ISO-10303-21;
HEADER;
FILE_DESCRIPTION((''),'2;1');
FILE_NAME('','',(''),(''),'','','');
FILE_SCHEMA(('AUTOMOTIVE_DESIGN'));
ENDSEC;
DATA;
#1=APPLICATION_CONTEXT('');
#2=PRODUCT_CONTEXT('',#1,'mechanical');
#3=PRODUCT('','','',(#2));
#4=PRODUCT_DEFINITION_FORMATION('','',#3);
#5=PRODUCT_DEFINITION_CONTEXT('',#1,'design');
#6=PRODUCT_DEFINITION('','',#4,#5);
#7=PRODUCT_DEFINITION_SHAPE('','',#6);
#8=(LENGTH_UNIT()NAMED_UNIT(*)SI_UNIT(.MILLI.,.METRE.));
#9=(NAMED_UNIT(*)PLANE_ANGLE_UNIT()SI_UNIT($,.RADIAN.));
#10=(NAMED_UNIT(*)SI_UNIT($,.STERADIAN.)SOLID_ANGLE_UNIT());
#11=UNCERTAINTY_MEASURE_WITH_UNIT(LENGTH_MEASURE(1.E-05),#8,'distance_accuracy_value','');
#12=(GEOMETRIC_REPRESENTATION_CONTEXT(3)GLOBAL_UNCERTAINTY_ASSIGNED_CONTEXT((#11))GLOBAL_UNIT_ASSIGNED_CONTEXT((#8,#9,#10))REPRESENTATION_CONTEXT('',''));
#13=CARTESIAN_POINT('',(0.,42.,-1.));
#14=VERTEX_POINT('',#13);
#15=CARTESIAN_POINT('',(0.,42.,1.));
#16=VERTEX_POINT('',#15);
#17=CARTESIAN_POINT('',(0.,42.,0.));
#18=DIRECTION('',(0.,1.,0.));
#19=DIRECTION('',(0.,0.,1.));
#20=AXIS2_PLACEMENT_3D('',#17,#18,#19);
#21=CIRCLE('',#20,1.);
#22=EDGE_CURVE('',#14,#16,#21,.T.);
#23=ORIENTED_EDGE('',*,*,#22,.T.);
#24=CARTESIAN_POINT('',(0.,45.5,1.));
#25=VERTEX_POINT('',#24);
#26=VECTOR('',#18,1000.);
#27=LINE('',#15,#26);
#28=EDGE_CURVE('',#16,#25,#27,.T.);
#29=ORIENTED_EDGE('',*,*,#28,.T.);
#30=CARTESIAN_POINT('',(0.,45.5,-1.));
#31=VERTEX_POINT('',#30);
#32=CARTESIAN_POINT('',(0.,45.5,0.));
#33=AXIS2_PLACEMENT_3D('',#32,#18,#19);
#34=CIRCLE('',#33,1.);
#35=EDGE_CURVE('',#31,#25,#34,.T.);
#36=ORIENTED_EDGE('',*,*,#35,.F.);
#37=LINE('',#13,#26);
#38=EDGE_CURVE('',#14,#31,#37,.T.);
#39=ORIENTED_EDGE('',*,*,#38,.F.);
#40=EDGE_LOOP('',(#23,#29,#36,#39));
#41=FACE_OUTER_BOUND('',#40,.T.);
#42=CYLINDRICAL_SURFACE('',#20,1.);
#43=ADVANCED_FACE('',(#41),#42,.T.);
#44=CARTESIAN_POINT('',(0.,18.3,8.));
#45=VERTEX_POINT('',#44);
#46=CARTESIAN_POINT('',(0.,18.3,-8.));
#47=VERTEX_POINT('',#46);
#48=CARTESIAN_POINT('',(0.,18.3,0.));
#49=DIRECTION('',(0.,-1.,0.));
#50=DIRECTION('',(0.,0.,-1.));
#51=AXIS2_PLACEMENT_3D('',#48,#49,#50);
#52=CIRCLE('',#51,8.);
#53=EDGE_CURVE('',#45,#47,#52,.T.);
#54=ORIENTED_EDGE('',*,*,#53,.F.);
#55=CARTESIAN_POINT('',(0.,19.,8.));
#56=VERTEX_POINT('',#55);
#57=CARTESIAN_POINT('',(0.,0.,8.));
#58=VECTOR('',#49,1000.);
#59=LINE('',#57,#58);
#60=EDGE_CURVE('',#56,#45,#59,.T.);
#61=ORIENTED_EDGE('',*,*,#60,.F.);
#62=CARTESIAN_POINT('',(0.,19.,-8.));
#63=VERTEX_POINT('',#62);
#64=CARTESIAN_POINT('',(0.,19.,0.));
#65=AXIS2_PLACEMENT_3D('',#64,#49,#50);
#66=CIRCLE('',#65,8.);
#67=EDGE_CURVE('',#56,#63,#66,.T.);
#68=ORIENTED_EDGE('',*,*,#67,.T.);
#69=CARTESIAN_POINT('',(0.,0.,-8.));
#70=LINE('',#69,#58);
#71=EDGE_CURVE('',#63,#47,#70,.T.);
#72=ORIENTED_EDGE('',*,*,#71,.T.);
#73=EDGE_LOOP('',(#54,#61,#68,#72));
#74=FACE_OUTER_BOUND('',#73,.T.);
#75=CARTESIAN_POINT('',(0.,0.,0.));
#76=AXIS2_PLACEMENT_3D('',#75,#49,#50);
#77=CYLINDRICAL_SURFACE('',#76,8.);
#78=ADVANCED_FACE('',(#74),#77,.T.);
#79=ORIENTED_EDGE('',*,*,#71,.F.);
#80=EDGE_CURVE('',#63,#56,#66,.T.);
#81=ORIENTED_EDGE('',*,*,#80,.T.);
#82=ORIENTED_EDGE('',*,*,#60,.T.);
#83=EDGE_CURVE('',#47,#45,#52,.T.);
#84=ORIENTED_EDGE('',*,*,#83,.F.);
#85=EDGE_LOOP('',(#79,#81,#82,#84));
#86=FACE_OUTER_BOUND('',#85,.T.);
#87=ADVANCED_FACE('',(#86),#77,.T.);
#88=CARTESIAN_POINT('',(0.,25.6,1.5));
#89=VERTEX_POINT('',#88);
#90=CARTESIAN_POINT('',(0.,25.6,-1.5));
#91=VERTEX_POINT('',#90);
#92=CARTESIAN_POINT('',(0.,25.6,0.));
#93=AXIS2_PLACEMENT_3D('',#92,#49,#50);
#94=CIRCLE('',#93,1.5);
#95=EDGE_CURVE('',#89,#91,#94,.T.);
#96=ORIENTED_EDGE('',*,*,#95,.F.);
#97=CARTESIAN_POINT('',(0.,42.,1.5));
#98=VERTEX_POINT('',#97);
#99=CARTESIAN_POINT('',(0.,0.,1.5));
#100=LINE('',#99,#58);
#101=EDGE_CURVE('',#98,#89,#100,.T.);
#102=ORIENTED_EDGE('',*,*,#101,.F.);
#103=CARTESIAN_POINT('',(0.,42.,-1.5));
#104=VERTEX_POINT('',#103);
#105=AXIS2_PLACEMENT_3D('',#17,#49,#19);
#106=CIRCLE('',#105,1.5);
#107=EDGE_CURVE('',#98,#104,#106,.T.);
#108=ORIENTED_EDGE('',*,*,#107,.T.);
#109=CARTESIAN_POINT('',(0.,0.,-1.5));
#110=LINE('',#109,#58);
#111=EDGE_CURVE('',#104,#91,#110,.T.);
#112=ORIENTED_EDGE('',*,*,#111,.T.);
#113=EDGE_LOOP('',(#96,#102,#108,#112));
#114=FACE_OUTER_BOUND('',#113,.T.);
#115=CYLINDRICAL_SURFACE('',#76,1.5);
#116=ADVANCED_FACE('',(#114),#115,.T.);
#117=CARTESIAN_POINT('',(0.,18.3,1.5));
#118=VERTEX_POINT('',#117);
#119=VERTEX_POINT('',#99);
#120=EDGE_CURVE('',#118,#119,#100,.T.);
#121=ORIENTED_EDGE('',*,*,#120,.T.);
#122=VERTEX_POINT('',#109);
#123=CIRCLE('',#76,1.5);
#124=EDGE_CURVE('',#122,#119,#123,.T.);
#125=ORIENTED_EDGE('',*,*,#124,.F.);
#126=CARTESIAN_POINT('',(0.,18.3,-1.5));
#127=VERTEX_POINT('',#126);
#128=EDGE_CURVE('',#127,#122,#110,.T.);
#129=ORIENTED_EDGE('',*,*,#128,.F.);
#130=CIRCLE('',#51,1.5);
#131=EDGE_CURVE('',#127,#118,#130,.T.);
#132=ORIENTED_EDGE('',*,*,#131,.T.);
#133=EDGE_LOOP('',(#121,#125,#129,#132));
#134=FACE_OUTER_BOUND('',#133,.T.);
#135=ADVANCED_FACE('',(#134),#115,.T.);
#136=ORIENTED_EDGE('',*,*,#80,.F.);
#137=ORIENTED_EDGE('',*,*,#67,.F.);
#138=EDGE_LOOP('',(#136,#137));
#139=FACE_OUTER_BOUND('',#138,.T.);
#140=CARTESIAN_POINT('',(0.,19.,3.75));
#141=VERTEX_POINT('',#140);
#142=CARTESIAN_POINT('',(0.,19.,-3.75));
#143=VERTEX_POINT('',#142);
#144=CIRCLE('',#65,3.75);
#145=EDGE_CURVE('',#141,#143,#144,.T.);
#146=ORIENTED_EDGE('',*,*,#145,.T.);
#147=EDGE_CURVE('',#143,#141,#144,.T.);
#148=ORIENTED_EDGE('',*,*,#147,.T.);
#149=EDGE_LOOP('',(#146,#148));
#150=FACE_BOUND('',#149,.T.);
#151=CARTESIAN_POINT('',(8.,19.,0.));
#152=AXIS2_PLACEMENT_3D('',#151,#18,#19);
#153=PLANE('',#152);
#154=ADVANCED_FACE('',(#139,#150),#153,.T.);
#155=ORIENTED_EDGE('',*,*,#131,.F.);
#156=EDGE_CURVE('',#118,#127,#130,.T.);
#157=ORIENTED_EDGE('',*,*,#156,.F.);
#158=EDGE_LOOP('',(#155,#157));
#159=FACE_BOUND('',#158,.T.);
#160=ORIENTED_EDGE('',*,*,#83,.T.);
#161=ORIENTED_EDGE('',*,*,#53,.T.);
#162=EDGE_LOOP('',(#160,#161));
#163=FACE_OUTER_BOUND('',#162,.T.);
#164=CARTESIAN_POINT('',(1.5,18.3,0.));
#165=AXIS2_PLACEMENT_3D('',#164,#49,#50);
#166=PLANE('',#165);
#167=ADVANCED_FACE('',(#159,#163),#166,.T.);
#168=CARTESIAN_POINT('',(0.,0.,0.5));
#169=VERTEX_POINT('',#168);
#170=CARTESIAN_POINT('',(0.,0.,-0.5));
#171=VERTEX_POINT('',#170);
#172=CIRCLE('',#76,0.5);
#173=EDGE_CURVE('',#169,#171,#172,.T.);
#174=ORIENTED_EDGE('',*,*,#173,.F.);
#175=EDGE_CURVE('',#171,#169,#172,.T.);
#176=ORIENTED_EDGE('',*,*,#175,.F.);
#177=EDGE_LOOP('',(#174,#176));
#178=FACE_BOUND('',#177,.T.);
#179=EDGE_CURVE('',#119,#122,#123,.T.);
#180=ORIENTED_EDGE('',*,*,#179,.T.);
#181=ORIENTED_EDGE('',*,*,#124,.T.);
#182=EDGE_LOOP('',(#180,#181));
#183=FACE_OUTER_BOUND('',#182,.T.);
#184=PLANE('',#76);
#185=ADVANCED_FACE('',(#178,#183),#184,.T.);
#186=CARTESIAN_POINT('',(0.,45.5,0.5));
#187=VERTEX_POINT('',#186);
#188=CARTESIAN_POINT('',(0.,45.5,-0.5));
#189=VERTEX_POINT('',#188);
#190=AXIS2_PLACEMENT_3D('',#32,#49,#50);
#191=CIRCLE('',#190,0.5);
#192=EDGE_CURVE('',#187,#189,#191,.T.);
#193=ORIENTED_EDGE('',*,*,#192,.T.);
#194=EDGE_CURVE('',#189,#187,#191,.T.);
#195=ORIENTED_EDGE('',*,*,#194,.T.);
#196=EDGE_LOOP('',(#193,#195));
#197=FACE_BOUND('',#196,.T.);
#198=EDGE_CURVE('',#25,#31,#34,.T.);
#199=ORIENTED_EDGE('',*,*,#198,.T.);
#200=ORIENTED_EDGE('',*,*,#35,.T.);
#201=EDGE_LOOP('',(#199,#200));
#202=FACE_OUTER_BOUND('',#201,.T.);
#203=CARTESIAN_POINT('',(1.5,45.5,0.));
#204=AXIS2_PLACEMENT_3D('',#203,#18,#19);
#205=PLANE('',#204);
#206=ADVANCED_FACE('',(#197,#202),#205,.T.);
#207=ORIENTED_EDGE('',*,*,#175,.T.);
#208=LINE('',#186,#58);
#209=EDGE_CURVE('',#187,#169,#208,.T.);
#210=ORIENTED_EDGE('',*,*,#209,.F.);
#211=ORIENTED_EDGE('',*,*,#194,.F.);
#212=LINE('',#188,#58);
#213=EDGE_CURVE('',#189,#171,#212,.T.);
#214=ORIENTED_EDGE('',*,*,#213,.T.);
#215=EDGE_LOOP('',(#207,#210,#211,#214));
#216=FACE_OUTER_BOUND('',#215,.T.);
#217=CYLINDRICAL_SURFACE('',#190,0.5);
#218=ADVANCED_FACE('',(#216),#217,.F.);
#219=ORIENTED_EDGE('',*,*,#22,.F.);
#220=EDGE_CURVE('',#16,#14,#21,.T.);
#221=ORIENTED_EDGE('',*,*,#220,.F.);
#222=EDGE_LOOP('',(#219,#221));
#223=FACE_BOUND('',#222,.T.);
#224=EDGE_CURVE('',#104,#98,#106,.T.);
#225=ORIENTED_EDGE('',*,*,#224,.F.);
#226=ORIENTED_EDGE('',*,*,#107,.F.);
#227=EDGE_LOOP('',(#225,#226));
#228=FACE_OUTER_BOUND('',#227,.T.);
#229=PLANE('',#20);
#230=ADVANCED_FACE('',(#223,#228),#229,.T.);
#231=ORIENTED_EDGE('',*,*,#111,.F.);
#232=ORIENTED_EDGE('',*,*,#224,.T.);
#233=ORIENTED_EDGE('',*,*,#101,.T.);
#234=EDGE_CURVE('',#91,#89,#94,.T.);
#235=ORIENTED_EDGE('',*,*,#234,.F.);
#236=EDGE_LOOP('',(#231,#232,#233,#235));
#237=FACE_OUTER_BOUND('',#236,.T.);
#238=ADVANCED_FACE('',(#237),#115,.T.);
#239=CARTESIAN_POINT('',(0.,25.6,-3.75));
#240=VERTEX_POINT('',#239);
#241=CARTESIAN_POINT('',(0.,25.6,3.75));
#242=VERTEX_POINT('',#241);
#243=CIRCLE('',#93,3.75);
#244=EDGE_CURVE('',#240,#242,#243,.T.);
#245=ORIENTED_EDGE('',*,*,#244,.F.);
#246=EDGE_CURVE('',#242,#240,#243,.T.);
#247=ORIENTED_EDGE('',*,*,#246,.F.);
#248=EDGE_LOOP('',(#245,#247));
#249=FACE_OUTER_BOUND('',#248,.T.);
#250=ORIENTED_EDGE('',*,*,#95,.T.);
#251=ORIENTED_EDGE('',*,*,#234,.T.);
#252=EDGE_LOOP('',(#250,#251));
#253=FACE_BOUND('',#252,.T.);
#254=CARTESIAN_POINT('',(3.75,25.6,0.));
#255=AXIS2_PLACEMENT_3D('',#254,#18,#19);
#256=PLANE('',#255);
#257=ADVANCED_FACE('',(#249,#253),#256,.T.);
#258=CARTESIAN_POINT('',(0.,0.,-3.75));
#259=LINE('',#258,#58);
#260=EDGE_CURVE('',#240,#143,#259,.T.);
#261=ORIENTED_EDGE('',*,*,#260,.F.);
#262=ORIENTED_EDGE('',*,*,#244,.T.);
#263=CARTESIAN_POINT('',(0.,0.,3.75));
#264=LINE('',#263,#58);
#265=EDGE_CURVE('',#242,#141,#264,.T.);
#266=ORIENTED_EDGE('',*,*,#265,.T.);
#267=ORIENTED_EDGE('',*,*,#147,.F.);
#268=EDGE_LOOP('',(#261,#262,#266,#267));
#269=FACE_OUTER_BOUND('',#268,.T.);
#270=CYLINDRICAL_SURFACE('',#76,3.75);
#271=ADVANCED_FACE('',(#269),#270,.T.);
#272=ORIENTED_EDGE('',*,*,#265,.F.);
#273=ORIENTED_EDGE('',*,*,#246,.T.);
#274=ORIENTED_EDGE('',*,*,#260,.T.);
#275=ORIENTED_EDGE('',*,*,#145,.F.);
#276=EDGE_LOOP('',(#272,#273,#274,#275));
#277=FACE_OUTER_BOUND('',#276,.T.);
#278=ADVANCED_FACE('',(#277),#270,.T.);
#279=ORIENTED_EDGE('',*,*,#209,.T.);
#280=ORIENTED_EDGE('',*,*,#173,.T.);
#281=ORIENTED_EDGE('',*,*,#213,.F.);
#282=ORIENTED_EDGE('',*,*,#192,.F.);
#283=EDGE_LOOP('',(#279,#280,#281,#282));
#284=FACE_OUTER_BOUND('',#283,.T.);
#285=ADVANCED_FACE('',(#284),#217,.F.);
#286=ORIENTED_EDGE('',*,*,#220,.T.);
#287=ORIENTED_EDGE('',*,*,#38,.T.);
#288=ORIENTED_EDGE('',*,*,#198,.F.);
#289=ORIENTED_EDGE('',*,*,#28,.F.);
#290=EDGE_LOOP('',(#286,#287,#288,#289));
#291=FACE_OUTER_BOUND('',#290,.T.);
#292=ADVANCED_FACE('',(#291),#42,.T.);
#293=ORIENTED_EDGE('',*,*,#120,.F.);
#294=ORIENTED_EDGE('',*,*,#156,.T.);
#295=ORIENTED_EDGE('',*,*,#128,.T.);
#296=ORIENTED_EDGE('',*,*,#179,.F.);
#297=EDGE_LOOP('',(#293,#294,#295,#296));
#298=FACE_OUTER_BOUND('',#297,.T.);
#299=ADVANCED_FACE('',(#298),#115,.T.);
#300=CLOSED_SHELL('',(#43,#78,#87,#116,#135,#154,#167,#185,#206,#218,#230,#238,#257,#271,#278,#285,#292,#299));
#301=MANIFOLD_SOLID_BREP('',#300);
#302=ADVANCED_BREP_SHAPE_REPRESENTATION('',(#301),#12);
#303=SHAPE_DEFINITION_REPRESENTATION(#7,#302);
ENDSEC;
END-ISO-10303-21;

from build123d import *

# Parameters (mm, degrees)
SKETCH3_R          = 0.5
CUT_EXTRUDE1_DEPTH = 47.885498824
SKETCH4_OUTSIDE_W  = 28.164
SKETCH4_OUTSIDE_H  = 28.164
SKETCH4_OUTSIDE_R  = 1
CUT_EXTRUDE2_DEPTH = 3.5


with BuildPart() as part:
    # Sketch1 → Revolve1 (revolve)
    with BuildSketch(Plane.XY, mode=Mode.PRIVATE) as revolve1_sk:
        Polygon((0, 0), (1.5, 0), (1.5, 18.3), (8, 18.3), (8, 19), (3.75, 19), (3.75, 25.6), (1.5, 25.6), (1.5, 45.5), (0, 45.5), align=None)
    revolve(revolve1_sk.sketch.rotate(Axis((0, 0, 0), (0, 1, 0)), 90), axis=Axis((0, 0, 0), (0, 1, 0)))

    # Sketch3 → Cut-Extrude1 (cut, through all)
    with BuildSketch(Plane.XZ):
        with Locations(Location((0, 0, 0), (0, 0, 270))):
            Circle(SKETCH3_R)
    extrude(amount=-CUT_EXTRUDE1_DEPTH, mode=Mode.SUBTRACT)

    # Sketch4 outside → Cut-Extrude2 (cut)
    with BuildSketch(Plane(origin=(0, 45.5, 0), x_dir=(1, 0, 0), z_dir=(0, 1, 0))):
        Rectangle(SKETCH4_OUTSIDE_W, SKETCH4_OUTSIDE_H)
        with Locations(Location((0, 0, 0), (0, 0, 270))):
            Circle(SKETCH4_OUTSIDE_R, mode=Mode.SUBTRACT)
    extrude(amount=-CUT_EXTRUDE2_DEPTH, mode=Mode.SUBTRACT)


solid = part.part
